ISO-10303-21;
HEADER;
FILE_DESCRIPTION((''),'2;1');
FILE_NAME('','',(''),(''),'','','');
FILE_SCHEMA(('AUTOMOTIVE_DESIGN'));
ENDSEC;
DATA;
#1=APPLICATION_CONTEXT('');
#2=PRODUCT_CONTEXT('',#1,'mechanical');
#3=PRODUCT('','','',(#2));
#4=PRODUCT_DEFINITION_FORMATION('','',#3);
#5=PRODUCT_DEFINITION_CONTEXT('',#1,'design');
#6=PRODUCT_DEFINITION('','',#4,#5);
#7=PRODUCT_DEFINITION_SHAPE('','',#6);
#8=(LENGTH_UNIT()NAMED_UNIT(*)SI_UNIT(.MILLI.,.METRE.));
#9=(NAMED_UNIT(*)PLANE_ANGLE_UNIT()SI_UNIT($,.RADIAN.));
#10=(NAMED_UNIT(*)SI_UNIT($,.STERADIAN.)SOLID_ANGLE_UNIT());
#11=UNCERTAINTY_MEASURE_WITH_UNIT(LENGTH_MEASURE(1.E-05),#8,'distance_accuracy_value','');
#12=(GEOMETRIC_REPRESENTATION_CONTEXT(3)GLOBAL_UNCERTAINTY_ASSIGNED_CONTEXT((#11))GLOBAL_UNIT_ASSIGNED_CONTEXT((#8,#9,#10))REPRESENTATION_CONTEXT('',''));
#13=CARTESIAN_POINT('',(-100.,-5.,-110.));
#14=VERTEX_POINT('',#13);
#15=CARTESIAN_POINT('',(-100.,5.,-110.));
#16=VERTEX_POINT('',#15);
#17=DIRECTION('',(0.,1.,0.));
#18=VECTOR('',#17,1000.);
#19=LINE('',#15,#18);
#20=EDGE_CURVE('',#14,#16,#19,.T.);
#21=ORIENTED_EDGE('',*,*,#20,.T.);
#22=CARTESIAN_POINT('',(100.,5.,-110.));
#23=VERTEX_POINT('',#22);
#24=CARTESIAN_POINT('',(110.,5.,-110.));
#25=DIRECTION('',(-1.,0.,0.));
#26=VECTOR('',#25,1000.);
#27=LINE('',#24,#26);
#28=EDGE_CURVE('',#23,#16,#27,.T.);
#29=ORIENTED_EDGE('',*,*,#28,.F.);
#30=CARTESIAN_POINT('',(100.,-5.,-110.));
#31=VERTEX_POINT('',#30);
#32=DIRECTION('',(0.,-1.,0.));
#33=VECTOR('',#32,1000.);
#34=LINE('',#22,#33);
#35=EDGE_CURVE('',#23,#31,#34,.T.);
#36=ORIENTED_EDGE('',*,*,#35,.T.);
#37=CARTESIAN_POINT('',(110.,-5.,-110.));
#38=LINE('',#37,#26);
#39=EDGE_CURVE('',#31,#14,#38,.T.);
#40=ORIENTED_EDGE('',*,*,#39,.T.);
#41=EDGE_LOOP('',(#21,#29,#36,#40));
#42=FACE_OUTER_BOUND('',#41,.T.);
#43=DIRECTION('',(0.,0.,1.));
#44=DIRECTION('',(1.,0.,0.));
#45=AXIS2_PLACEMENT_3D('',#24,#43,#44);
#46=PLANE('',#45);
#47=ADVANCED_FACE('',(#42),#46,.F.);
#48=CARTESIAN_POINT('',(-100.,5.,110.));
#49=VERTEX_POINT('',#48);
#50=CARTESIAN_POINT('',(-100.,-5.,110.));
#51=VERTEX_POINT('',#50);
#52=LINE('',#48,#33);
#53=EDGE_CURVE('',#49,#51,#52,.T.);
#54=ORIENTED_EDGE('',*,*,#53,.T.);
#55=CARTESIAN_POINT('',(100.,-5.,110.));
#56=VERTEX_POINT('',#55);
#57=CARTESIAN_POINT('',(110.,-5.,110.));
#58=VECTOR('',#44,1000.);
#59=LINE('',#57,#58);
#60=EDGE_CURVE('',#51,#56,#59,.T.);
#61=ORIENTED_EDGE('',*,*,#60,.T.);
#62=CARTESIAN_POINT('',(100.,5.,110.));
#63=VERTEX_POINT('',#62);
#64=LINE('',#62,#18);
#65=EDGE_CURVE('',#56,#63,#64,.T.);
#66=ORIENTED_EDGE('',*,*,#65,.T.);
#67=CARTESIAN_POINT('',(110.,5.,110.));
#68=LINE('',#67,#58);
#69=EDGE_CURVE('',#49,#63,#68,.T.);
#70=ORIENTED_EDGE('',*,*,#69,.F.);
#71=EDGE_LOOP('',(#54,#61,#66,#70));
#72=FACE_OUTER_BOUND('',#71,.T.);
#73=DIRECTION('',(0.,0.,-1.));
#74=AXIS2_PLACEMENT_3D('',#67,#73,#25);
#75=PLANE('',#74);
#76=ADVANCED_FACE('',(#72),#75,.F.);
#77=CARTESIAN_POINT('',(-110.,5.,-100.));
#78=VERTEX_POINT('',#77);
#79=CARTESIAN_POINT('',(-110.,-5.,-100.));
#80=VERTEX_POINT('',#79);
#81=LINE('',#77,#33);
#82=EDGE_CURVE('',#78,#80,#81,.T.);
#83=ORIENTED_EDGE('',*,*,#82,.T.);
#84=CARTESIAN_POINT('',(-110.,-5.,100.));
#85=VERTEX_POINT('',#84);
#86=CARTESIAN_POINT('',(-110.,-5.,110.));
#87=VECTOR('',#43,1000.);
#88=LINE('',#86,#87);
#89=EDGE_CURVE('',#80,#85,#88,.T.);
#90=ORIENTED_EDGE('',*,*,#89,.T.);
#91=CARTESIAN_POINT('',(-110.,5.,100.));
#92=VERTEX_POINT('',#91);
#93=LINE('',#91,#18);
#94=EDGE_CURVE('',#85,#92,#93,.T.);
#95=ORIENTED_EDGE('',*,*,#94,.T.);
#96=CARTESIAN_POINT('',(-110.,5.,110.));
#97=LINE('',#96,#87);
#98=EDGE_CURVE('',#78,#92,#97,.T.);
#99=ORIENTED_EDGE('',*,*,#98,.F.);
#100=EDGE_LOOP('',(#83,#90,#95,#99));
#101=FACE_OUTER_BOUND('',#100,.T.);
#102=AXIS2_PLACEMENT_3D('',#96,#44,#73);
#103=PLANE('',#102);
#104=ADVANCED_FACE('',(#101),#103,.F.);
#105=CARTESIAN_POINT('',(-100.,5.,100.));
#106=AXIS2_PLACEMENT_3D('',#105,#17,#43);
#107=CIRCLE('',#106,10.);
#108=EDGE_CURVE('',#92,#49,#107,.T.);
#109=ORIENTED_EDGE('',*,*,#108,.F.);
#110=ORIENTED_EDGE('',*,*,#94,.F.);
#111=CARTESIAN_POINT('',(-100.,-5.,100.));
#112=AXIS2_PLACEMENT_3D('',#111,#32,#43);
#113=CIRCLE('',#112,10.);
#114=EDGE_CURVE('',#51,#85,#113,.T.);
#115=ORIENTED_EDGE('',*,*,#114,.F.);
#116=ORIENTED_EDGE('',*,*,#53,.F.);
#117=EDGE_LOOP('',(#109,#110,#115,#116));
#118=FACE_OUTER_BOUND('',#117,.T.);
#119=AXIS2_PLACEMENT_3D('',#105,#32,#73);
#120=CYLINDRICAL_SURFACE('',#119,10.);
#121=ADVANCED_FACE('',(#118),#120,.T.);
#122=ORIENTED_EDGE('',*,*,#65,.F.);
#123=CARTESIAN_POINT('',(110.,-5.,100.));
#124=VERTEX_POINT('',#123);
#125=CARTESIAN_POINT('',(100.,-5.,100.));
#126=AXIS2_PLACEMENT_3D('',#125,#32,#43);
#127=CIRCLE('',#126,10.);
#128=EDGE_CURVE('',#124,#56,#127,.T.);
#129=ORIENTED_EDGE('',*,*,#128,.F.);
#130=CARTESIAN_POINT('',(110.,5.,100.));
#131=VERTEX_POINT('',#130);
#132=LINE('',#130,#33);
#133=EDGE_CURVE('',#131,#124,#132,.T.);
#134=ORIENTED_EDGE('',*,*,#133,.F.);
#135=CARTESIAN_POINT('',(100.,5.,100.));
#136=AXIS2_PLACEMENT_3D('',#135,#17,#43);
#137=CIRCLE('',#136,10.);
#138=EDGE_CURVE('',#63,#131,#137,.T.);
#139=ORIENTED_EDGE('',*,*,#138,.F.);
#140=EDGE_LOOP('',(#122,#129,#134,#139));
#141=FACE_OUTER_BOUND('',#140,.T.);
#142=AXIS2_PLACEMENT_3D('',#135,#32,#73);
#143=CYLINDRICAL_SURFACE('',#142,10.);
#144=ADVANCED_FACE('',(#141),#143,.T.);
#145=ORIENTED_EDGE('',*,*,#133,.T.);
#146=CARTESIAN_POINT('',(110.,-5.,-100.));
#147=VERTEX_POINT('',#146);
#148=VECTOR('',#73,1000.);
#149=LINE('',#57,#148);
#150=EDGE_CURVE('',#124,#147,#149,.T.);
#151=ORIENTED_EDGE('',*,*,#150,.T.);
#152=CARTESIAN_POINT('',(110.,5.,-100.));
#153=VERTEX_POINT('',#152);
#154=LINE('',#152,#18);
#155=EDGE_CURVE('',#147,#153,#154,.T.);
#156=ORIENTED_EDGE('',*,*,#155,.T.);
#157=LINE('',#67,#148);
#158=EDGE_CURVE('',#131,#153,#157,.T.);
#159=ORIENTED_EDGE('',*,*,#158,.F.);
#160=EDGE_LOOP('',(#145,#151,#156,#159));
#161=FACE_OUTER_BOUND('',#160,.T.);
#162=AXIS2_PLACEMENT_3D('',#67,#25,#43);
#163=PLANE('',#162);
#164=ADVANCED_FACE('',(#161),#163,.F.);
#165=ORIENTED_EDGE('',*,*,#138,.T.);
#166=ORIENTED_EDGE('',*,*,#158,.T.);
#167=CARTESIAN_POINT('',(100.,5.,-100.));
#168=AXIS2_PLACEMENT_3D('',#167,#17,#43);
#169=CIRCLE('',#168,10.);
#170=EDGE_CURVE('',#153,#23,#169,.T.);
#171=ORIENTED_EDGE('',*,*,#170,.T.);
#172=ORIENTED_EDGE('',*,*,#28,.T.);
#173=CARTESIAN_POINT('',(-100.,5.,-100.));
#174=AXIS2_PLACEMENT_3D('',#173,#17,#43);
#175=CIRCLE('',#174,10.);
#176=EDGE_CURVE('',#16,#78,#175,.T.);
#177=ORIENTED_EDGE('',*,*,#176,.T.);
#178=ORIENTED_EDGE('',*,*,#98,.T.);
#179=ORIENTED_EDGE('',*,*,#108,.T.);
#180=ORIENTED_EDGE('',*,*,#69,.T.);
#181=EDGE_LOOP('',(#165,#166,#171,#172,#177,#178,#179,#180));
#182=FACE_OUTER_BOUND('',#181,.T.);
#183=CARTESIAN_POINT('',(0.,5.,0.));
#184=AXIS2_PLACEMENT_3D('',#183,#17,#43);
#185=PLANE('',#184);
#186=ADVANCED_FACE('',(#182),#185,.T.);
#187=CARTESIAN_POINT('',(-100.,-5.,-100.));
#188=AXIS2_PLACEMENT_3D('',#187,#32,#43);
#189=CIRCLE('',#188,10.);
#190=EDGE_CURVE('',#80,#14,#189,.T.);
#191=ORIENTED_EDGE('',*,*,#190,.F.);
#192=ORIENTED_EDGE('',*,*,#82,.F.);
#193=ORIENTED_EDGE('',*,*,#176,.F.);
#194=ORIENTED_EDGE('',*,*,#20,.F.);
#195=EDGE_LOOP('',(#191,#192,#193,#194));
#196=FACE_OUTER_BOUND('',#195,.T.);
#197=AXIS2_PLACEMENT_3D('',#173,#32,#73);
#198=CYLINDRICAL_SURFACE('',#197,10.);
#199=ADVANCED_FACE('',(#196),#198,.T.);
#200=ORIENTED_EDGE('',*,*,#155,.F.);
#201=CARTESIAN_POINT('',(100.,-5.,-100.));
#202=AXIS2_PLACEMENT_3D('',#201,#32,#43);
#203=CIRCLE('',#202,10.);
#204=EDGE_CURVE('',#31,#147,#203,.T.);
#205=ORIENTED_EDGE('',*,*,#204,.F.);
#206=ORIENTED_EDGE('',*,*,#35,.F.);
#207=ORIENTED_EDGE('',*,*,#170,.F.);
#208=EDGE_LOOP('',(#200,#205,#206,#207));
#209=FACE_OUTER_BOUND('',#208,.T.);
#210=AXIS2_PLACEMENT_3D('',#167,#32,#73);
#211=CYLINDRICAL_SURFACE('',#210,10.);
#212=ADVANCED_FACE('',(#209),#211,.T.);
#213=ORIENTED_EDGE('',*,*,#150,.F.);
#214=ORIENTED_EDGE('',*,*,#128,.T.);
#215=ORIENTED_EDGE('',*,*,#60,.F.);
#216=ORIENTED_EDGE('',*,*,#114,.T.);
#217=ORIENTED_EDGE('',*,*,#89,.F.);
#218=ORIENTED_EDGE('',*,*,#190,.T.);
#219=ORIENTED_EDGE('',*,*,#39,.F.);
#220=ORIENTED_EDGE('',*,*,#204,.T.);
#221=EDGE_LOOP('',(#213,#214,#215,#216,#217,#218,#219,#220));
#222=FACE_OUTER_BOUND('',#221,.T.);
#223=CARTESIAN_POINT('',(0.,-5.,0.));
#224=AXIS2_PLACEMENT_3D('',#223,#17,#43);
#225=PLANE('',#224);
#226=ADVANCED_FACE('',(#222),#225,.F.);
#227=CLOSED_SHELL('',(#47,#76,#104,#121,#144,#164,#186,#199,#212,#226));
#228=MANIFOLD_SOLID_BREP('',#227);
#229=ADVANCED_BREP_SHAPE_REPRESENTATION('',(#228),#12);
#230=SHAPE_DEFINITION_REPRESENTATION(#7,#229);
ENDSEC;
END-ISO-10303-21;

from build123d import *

# Parameters (mm, degrees)
SKETCH_1_W      = 220
SKETCH_1_H      = 220
EXTRUDE_1_DEPTH = 5
FILLET_1_R      = 10


with BuildPart() as part:
    # 草图1 → 凸台-拉伸1 (new, symmetric)
    with BuildSketch(Plane(origin=(0, 0, 0), x_dir=(1, 0, 0), z_dir=(0, 1, 0))):
        Rectangle(SKETCH_1_W, SKETCH_1_H)
    extrude(amount=EXTRUDE_1_DEPTH, both=True)

    # 圆角1
    fillet_1_edges = [part.edges().sort_by_distance(p)[0] for p in [
        (-110, 0, -110),
        (110, 0, -110),
        (110, 0, 110),
        (-110, 0, 110),
    ]]
    fillet(fillet_1_edges, radius=FILLET_1_R)


solid = part.part
